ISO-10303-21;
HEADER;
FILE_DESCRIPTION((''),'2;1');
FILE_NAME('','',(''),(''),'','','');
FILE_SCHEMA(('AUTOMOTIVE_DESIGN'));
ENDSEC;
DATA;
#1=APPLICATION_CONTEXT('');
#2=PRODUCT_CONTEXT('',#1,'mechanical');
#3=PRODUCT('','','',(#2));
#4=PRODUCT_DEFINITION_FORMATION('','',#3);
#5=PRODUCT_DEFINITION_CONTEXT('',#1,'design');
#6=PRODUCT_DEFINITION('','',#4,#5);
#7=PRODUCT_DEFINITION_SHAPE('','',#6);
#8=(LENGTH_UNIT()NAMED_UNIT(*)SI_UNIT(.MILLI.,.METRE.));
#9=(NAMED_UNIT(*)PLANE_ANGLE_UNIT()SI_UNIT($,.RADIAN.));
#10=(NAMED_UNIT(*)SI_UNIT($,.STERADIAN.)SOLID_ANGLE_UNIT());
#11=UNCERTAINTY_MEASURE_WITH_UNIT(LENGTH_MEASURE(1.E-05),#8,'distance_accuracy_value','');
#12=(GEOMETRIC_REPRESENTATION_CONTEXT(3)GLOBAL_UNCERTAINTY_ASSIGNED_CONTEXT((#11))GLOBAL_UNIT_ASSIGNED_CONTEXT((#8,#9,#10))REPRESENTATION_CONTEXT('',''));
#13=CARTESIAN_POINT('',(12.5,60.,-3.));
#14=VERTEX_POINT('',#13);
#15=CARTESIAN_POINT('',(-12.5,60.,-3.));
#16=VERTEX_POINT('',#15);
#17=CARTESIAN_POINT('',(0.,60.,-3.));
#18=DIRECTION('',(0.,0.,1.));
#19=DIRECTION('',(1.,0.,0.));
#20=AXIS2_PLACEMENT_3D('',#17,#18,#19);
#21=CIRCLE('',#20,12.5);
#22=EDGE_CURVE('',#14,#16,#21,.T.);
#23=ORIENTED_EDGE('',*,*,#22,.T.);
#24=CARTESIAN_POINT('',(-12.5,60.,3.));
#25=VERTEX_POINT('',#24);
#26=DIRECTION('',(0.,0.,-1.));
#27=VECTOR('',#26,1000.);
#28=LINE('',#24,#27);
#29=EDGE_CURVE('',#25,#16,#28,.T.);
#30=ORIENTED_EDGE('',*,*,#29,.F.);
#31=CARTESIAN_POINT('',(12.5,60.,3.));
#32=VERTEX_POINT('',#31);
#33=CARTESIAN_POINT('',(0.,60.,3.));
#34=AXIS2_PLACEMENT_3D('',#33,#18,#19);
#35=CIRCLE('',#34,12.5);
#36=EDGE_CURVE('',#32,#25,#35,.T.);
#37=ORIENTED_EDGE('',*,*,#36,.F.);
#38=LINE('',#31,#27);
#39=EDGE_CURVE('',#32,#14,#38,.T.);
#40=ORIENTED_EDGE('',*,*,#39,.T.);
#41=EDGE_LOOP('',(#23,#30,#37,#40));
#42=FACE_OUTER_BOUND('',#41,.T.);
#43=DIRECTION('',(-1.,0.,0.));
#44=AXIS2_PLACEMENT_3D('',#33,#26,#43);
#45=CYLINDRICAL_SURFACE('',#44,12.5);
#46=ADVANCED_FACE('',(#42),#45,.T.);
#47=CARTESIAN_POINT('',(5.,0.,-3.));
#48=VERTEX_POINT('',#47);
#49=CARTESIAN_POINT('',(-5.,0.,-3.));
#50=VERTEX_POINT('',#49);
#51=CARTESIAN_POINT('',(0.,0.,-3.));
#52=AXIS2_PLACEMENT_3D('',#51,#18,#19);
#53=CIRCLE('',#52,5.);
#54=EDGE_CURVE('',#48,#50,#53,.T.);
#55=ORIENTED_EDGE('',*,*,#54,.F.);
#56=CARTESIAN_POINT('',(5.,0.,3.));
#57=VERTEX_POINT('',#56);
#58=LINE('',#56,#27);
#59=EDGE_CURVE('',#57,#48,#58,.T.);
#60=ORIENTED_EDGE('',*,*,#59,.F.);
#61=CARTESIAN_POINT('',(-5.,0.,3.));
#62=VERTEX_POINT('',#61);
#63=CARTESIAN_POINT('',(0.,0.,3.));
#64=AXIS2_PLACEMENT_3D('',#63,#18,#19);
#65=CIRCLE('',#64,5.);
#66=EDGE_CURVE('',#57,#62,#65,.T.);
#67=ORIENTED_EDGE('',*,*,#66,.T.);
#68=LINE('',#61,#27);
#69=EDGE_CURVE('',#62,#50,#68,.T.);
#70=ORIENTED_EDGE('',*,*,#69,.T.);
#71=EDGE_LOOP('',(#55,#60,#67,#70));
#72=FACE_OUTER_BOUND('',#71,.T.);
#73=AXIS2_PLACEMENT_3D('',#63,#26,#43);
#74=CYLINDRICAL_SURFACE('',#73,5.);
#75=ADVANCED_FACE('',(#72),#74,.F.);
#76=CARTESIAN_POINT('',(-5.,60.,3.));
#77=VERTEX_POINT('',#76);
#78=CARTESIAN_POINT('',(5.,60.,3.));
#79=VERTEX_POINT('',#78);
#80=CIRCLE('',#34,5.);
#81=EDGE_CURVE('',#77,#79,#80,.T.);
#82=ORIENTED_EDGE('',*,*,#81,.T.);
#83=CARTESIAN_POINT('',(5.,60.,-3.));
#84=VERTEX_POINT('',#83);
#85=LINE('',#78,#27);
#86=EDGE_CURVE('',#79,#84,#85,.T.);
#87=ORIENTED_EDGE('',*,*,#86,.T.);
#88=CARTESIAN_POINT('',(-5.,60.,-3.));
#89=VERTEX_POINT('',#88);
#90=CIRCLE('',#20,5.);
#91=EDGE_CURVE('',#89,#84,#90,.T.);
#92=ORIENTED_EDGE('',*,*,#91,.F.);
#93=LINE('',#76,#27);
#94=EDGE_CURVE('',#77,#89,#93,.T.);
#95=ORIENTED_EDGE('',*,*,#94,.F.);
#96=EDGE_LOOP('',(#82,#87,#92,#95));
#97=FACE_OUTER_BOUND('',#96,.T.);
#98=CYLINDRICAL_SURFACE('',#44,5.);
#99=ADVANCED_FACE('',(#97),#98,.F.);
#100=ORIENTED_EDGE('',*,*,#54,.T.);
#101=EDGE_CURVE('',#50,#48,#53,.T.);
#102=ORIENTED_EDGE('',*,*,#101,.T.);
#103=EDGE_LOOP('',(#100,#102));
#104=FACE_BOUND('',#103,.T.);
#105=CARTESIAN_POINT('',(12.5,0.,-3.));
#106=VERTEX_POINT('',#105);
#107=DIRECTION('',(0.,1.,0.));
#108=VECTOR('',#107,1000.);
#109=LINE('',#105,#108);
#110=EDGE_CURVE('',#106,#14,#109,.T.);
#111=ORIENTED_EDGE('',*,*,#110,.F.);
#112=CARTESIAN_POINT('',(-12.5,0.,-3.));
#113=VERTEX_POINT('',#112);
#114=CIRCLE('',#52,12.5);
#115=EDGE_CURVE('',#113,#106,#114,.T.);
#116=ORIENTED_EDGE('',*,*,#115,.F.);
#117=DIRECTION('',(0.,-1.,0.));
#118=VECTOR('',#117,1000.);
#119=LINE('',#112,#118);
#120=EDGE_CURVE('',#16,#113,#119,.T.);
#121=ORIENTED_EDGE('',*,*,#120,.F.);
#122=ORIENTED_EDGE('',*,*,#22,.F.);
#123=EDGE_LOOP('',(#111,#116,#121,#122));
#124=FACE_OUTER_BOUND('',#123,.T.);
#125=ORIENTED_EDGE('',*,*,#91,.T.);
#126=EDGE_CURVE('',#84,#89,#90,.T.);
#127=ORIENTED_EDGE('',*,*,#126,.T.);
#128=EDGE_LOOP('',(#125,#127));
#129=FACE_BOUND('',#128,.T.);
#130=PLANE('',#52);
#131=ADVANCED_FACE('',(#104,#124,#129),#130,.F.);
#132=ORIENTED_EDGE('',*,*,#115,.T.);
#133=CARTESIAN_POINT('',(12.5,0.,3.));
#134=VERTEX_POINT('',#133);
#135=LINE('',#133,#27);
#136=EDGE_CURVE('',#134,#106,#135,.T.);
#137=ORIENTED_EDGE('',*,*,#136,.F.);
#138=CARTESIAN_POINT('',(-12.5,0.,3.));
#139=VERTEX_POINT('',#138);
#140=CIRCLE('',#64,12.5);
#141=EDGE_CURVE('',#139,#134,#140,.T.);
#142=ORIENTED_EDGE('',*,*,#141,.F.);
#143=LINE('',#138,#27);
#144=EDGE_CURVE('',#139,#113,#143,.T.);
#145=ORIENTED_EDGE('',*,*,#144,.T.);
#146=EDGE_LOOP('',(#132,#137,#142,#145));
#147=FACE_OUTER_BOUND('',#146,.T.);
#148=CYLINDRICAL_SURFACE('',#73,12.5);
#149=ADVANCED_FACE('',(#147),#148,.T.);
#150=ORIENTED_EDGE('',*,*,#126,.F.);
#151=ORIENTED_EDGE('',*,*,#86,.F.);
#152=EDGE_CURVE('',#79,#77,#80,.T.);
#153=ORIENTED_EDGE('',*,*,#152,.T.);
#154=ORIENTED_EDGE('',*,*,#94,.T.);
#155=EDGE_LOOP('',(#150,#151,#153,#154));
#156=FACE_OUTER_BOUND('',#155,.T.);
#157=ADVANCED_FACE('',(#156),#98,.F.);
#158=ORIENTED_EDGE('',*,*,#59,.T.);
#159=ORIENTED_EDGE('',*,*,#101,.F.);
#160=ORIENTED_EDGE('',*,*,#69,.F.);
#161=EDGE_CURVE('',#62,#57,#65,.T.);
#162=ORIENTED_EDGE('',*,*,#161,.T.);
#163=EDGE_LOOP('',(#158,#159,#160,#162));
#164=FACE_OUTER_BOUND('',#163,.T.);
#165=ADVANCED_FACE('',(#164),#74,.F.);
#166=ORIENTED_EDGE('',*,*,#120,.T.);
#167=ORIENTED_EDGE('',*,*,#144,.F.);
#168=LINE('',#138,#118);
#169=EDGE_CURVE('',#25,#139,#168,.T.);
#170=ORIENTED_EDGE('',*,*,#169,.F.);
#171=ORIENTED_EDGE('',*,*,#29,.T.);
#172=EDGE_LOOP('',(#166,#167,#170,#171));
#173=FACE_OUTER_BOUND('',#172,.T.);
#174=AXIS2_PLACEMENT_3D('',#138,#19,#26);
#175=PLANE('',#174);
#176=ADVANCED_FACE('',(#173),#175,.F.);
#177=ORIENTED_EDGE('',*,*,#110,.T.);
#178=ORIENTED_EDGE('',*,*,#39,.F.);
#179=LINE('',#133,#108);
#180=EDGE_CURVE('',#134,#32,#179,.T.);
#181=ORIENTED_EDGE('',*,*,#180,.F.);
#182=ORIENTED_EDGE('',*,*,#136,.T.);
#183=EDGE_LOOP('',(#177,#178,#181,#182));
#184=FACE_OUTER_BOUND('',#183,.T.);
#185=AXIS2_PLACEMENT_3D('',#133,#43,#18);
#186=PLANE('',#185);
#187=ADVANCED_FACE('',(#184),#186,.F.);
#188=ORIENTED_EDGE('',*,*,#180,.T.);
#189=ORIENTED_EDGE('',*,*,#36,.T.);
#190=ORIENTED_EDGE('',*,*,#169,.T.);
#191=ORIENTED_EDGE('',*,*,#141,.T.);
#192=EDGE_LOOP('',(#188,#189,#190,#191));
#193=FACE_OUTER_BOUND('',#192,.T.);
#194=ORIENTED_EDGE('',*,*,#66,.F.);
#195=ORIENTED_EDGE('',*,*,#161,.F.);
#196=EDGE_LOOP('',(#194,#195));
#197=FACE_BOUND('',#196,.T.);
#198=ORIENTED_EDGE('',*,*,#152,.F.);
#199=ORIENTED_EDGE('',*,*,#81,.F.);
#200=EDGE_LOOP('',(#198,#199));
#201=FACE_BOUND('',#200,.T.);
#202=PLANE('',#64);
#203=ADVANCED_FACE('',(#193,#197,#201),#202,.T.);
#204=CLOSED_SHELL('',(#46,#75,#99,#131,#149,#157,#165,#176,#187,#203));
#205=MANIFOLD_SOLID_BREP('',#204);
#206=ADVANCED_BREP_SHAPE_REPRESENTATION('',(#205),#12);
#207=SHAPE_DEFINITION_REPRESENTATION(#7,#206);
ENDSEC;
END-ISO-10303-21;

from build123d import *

# Parameters (mm, degrees)
SKETCH1_R           = 5
BOSS_EXTRUDE1_DEPTH = 3


with BuildPart() as part:
    # Sketch1 → Boss-Extrude1 (new, symmetric)
    with BuildSketch(Plane.XY):
        with BuildLine():
            Line((-12.5, 0), (-12.5, 60))
            ThreePointArc((-12.5, 60), (0, 72.5), (12.5, 60))
            Line((12.5, 60), (12.5, 0))
            ThreePointArc((12.5, 0), (0, -12.5), (-12.5, 0))
        make_face()
        Circle(SKETCH1_R, mode=Mode.SUBTRACT)
        with Locations((0, 60)):
            Circle(SKETCH1_R, mode=Mode.SUBTRACT)
    extrude(amount=BOSS_EXTRUDE1_DEPTH, both=True)


solid = part.part
